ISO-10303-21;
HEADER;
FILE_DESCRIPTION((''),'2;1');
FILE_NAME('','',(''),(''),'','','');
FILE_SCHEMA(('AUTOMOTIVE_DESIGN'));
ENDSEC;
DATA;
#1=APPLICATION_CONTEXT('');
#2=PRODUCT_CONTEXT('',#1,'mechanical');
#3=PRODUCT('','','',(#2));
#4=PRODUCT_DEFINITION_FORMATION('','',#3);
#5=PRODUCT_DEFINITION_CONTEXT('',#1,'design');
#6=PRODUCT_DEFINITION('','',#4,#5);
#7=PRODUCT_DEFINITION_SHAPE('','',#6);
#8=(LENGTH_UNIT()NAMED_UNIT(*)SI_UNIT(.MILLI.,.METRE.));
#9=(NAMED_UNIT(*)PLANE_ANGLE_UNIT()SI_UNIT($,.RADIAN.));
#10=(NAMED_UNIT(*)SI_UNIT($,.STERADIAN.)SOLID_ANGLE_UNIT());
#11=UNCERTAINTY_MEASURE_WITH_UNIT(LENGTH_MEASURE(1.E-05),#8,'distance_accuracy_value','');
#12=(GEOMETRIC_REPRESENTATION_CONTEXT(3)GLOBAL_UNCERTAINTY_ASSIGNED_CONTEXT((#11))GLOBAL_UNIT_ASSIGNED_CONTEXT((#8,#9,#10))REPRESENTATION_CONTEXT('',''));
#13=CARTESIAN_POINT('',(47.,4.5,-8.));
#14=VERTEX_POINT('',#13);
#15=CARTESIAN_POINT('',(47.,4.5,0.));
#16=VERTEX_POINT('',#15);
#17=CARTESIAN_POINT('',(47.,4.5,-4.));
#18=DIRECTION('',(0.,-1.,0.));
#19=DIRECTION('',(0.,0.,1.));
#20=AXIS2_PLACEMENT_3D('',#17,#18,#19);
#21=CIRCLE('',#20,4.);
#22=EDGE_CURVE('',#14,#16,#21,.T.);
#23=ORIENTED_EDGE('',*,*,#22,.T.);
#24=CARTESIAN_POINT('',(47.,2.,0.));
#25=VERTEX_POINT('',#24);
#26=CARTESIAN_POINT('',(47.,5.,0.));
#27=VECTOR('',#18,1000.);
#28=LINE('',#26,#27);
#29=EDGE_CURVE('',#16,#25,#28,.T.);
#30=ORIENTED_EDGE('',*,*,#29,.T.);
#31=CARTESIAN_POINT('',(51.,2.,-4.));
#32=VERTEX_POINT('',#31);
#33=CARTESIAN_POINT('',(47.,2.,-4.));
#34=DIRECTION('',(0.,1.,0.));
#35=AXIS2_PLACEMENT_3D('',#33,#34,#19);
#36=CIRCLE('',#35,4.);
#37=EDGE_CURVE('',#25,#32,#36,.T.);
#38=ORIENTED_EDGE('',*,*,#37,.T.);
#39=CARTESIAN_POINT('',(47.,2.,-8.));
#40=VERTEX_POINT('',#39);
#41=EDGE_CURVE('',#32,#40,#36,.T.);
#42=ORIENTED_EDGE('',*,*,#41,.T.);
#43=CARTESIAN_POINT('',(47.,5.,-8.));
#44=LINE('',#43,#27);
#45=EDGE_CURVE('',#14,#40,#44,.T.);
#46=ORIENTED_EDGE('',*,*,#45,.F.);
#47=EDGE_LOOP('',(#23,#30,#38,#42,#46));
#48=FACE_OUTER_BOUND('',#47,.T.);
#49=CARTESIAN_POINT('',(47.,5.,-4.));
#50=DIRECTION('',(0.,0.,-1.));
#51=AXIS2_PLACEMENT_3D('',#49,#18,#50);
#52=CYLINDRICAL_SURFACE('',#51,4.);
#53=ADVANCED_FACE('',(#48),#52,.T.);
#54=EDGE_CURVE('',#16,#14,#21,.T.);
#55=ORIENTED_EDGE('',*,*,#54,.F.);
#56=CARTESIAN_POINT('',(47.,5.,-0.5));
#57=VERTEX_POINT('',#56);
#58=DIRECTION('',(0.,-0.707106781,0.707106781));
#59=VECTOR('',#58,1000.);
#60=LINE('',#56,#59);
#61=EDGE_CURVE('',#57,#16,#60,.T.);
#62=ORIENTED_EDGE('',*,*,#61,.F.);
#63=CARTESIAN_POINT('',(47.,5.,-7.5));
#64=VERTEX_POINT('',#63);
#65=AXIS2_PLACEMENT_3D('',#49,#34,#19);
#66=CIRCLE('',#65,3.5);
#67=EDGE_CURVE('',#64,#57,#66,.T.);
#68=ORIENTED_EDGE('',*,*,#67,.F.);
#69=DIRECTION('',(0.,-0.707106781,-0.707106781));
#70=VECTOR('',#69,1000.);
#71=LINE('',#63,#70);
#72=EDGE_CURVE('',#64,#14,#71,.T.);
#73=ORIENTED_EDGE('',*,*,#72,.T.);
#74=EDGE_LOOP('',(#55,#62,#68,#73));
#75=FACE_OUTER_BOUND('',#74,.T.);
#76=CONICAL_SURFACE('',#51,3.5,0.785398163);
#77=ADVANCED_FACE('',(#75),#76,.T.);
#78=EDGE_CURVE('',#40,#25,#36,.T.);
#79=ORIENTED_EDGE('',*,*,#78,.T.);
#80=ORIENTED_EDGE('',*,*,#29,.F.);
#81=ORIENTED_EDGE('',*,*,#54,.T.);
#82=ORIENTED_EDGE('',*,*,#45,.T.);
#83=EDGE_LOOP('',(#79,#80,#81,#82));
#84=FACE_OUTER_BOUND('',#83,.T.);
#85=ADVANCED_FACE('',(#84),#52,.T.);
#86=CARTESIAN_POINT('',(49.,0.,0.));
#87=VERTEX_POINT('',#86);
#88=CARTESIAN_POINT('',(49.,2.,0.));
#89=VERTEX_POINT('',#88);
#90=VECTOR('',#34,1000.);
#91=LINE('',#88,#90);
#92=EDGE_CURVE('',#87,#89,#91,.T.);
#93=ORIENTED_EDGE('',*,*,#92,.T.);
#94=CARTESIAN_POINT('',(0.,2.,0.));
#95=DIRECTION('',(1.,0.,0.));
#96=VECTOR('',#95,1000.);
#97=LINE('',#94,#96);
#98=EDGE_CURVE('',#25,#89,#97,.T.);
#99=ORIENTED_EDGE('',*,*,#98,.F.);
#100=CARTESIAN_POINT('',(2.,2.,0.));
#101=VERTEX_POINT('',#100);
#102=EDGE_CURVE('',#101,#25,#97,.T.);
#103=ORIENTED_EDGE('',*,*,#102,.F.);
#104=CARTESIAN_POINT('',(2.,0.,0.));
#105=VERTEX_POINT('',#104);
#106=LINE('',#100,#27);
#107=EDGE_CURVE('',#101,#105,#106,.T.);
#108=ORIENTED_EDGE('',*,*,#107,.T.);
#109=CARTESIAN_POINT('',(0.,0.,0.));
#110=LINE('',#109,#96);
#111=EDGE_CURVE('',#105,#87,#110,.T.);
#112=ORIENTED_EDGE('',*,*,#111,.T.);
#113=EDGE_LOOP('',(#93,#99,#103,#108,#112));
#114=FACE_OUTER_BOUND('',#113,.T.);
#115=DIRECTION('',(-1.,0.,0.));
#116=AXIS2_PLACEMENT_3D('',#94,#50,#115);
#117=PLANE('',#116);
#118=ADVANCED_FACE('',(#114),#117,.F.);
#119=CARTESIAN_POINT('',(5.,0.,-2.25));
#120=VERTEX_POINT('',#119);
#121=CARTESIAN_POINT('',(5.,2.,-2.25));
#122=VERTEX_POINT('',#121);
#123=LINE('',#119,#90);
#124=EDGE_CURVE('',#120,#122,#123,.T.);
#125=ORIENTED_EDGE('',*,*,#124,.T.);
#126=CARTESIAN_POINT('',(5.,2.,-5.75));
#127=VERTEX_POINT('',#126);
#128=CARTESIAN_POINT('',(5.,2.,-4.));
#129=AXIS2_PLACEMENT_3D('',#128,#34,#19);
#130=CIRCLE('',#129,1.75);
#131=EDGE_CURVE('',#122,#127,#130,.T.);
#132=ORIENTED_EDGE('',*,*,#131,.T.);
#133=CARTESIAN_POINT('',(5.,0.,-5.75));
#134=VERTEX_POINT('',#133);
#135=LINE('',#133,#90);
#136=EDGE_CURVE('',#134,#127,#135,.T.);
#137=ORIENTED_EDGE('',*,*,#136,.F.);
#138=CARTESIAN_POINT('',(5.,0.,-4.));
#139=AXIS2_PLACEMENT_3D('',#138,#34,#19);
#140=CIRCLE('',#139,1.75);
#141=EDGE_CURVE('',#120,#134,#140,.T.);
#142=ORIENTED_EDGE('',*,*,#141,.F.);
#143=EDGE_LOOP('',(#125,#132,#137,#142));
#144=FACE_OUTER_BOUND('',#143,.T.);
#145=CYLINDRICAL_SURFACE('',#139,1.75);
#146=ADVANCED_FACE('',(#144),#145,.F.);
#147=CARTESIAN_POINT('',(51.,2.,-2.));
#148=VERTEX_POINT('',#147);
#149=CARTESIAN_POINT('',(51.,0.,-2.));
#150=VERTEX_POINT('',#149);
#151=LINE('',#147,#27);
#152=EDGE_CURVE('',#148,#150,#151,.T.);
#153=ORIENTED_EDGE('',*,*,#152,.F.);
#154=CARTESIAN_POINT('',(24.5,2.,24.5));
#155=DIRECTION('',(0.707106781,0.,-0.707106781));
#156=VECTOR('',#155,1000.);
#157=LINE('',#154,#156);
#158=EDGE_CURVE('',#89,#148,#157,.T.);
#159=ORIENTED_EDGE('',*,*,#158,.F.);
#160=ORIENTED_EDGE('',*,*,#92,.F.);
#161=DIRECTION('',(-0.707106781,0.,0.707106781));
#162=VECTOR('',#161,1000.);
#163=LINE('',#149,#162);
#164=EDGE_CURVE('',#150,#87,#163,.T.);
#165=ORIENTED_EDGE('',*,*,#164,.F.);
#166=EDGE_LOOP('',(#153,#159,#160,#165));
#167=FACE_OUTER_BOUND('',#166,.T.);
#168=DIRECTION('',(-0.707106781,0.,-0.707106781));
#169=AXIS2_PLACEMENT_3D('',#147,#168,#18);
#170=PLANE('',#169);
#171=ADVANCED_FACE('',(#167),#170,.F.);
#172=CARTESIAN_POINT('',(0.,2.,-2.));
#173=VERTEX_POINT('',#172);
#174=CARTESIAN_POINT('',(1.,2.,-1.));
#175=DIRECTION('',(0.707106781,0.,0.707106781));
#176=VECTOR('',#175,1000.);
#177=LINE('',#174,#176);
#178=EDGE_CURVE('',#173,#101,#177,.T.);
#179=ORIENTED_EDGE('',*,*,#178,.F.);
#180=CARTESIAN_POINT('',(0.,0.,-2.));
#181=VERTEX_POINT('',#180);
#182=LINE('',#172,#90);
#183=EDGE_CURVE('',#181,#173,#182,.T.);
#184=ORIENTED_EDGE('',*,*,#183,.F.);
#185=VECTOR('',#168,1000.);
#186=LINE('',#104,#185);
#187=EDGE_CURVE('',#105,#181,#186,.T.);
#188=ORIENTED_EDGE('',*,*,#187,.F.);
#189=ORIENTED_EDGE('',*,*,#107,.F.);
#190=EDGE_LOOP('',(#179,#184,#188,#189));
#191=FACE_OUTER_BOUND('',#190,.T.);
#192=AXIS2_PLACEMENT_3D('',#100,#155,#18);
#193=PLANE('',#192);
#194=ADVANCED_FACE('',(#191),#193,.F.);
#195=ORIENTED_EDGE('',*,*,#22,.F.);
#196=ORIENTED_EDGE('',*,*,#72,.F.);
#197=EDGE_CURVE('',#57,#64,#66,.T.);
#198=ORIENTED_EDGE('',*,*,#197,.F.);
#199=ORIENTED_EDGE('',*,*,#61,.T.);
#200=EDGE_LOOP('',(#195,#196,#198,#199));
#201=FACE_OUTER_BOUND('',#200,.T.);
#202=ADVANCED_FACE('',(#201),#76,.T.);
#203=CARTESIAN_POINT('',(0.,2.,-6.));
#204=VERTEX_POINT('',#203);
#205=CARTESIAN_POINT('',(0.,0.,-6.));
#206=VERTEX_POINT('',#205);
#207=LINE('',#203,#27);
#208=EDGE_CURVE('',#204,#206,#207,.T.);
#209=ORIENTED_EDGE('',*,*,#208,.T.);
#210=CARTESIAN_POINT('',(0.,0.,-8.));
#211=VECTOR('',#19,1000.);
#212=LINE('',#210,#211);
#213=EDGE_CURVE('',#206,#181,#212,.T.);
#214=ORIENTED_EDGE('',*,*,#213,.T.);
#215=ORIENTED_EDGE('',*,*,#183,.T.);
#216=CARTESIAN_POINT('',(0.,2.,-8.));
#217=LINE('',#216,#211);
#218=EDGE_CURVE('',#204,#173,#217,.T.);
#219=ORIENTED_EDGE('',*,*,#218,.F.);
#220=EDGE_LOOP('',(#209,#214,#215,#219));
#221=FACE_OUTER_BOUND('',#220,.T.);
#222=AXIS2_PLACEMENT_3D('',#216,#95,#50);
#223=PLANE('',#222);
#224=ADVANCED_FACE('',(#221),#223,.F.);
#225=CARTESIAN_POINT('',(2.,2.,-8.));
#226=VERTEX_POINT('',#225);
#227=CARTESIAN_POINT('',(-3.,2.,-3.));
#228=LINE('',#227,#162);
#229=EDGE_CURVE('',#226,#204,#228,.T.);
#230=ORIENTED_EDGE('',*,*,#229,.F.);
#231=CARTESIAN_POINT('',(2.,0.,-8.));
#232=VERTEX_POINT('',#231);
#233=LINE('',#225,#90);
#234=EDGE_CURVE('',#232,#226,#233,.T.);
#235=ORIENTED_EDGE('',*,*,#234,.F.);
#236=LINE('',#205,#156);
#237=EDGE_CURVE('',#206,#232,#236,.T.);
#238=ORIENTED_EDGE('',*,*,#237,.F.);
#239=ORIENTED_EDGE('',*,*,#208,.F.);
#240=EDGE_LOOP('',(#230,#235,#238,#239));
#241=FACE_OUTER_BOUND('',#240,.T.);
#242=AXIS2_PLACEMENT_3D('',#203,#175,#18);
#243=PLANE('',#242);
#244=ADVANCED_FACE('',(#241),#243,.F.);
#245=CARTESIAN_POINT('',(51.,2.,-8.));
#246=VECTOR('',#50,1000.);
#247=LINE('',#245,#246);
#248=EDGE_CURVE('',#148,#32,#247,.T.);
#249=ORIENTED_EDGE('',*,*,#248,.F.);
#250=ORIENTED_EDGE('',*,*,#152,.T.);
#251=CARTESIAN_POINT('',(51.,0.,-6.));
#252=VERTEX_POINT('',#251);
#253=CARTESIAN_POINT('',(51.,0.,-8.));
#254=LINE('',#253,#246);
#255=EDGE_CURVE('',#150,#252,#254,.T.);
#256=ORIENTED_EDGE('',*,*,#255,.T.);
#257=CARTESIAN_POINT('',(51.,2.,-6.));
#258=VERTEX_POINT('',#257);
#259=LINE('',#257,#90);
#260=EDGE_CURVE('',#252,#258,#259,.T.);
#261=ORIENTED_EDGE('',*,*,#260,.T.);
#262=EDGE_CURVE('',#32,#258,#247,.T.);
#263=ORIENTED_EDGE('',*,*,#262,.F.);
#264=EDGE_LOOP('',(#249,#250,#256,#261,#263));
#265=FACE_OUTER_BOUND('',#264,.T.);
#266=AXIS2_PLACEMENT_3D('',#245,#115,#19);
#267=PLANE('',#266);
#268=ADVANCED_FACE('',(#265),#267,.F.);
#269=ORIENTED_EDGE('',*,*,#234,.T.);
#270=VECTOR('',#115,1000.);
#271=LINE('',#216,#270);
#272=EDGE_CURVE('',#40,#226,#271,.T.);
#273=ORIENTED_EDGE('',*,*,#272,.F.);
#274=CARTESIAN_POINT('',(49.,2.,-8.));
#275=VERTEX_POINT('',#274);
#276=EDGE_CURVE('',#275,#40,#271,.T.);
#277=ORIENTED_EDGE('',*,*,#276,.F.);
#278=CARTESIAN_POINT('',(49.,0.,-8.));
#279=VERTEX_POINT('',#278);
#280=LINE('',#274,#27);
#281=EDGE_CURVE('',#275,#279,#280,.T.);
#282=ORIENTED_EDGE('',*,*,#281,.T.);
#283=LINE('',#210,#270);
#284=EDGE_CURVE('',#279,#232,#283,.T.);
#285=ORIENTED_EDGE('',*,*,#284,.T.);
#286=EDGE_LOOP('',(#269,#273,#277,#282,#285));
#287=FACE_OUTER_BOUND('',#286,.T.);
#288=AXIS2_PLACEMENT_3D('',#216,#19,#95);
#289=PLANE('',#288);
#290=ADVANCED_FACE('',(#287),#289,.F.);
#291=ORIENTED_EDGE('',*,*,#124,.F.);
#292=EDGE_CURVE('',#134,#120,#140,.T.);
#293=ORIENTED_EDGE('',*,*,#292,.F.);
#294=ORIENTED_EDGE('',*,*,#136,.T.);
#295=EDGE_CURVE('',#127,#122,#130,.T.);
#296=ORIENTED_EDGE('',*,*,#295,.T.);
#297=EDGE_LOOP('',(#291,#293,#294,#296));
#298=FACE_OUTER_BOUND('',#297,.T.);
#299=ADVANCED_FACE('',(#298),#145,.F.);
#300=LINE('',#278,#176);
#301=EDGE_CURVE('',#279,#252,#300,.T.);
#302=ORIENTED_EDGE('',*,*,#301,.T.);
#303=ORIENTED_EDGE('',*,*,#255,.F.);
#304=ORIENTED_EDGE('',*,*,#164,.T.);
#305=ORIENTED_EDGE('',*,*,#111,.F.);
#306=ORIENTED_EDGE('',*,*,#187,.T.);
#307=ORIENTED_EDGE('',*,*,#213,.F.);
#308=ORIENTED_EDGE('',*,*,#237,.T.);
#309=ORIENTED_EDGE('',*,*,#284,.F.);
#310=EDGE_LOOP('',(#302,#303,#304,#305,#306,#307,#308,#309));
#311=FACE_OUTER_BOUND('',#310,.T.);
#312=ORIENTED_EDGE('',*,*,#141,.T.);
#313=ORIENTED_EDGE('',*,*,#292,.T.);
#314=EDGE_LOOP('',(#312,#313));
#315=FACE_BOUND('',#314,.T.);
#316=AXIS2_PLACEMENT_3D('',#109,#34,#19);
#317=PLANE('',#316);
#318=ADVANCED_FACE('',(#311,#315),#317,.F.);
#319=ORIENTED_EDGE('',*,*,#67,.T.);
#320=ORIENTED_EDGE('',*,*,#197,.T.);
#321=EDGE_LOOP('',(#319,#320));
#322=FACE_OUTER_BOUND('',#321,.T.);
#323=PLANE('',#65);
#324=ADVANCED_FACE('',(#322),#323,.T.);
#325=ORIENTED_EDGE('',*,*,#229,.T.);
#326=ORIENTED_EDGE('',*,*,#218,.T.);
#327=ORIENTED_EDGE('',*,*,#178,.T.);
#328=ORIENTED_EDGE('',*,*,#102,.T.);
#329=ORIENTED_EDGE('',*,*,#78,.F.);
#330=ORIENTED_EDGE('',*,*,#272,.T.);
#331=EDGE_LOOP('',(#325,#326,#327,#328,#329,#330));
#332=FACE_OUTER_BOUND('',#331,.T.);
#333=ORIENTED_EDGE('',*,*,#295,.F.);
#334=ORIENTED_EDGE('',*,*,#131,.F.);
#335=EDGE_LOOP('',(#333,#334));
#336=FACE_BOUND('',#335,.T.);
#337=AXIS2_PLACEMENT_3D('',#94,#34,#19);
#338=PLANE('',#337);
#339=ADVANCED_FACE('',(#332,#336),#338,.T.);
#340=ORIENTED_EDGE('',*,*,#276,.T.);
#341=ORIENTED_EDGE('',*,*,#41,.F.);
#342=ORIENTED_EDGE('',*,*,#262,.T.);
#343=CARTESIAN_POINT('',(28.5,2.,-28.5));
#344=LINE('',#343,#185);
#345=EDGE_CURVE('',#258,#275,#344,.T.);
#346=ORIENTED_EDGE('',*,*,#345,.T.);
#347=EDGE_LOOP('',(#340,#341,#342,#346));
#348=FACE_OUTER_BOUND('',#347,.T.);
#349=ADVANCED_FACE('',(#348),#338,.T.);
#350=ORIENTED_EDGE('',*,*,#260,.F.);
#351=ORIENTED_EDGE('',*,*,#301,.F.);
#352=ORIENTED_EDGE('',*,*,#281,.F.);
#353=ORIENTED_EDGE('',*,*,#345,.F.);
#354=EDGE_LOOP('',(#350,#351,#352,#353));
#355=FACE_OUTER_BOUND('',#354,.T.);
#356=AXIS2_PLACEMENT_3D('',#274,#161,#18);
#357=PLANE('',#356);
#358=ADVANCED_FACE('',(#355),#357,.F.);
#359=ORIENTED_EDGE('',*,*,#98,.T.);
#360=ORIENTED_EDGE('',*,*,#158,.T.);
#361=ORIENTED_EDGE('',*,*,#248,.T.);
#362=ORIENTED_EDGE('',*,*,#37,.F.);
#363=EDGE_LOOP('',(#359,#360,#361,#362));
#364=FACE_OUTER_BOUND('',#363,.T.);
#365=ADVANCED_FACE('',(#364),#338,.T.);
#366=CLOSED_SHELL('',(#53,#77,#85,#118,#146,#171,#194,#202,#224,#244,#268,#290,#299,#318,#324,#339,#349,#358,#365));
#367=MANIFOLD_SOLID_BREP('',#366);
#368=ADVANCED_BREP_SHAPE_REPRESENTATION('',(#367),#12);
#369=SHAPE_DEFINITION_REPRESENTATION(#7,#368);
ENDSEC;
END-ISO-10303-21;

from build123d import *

# Parameters (mm, degrees)
SKETCH1_W           = 51
SKETCH1_H           = 8
BOSS_EXTRUDE1_DEPTH = 2
SKETCH2_R           = 1.75
CUT_EXTRUDE1_DEPTH  = 52.662365412
SKETCH3_R           = 4
BOSS_EXTRUDE2_DEPTH = 3
CHAMFER1_SIZE       = 0.5
CHAMFER2_SIZE       = 2


with BuildPart() as part:
    # Sketch1 → Boss-Extrude1 (new body)
    with BuildSketch(Plane(origin=(0, 0, 0), x_dir=(1, 0, 0), z_dir=(0, 1, 0))):
        with Locations((25.5, 4)):
            Rectangle(SKETCH1_W, SKETCH1_H)
    extrude(amount=BOSS_EXTRUDE1_DEPTH)

    # Sketch2 → Cut-Extrude1 (cut, through all)
    with BuildSketch(Plane(origin=(0, 2, 0), x_dir=(1, 0, 0), z_dir=(0, 1, 0))):
        with Locations(Location((5, 4, 0), (0, 0, 270))):
            Circle(SKETCH2_R)
    extrude(amount=-CUT_EXTRUDE1_DEPTH, mode=Mode.SUBTRACT)

    # Sketch3 → Boss-Extrude2 (add)
    with BuildSketch(Plane(origin=(0, 2, 0), x_dir=(1, 0, 0), z_dir=(0, 1, 0))):
        with Locations(Location((47, 4, 0), (0, 0, 270))):
            Circle(SKETCH3_R)
    extrude(amount=BOSS_EXTRUDE2_DEPTH)

    # Chamfer1
    chamfer1_edges = [part.edges().sort_by_distance(p)[0] for p in [
        (47, 5, -8),
    ]]
    chamfer(chamfer1_edges, length=CHAMFER1_SIZE)

    # Chamfer2
    chamfer2_edges = [part.edges().sort_by_distance(p)[0] for p in [
        (0, 1, -8),
        (51, 1, -8),
        (51, 1, 0),
        (0, 1, 0),
    ]]
    chamfer(chamfer2_edges, length=CHAMFER2_SIZE)


solid = part.part
